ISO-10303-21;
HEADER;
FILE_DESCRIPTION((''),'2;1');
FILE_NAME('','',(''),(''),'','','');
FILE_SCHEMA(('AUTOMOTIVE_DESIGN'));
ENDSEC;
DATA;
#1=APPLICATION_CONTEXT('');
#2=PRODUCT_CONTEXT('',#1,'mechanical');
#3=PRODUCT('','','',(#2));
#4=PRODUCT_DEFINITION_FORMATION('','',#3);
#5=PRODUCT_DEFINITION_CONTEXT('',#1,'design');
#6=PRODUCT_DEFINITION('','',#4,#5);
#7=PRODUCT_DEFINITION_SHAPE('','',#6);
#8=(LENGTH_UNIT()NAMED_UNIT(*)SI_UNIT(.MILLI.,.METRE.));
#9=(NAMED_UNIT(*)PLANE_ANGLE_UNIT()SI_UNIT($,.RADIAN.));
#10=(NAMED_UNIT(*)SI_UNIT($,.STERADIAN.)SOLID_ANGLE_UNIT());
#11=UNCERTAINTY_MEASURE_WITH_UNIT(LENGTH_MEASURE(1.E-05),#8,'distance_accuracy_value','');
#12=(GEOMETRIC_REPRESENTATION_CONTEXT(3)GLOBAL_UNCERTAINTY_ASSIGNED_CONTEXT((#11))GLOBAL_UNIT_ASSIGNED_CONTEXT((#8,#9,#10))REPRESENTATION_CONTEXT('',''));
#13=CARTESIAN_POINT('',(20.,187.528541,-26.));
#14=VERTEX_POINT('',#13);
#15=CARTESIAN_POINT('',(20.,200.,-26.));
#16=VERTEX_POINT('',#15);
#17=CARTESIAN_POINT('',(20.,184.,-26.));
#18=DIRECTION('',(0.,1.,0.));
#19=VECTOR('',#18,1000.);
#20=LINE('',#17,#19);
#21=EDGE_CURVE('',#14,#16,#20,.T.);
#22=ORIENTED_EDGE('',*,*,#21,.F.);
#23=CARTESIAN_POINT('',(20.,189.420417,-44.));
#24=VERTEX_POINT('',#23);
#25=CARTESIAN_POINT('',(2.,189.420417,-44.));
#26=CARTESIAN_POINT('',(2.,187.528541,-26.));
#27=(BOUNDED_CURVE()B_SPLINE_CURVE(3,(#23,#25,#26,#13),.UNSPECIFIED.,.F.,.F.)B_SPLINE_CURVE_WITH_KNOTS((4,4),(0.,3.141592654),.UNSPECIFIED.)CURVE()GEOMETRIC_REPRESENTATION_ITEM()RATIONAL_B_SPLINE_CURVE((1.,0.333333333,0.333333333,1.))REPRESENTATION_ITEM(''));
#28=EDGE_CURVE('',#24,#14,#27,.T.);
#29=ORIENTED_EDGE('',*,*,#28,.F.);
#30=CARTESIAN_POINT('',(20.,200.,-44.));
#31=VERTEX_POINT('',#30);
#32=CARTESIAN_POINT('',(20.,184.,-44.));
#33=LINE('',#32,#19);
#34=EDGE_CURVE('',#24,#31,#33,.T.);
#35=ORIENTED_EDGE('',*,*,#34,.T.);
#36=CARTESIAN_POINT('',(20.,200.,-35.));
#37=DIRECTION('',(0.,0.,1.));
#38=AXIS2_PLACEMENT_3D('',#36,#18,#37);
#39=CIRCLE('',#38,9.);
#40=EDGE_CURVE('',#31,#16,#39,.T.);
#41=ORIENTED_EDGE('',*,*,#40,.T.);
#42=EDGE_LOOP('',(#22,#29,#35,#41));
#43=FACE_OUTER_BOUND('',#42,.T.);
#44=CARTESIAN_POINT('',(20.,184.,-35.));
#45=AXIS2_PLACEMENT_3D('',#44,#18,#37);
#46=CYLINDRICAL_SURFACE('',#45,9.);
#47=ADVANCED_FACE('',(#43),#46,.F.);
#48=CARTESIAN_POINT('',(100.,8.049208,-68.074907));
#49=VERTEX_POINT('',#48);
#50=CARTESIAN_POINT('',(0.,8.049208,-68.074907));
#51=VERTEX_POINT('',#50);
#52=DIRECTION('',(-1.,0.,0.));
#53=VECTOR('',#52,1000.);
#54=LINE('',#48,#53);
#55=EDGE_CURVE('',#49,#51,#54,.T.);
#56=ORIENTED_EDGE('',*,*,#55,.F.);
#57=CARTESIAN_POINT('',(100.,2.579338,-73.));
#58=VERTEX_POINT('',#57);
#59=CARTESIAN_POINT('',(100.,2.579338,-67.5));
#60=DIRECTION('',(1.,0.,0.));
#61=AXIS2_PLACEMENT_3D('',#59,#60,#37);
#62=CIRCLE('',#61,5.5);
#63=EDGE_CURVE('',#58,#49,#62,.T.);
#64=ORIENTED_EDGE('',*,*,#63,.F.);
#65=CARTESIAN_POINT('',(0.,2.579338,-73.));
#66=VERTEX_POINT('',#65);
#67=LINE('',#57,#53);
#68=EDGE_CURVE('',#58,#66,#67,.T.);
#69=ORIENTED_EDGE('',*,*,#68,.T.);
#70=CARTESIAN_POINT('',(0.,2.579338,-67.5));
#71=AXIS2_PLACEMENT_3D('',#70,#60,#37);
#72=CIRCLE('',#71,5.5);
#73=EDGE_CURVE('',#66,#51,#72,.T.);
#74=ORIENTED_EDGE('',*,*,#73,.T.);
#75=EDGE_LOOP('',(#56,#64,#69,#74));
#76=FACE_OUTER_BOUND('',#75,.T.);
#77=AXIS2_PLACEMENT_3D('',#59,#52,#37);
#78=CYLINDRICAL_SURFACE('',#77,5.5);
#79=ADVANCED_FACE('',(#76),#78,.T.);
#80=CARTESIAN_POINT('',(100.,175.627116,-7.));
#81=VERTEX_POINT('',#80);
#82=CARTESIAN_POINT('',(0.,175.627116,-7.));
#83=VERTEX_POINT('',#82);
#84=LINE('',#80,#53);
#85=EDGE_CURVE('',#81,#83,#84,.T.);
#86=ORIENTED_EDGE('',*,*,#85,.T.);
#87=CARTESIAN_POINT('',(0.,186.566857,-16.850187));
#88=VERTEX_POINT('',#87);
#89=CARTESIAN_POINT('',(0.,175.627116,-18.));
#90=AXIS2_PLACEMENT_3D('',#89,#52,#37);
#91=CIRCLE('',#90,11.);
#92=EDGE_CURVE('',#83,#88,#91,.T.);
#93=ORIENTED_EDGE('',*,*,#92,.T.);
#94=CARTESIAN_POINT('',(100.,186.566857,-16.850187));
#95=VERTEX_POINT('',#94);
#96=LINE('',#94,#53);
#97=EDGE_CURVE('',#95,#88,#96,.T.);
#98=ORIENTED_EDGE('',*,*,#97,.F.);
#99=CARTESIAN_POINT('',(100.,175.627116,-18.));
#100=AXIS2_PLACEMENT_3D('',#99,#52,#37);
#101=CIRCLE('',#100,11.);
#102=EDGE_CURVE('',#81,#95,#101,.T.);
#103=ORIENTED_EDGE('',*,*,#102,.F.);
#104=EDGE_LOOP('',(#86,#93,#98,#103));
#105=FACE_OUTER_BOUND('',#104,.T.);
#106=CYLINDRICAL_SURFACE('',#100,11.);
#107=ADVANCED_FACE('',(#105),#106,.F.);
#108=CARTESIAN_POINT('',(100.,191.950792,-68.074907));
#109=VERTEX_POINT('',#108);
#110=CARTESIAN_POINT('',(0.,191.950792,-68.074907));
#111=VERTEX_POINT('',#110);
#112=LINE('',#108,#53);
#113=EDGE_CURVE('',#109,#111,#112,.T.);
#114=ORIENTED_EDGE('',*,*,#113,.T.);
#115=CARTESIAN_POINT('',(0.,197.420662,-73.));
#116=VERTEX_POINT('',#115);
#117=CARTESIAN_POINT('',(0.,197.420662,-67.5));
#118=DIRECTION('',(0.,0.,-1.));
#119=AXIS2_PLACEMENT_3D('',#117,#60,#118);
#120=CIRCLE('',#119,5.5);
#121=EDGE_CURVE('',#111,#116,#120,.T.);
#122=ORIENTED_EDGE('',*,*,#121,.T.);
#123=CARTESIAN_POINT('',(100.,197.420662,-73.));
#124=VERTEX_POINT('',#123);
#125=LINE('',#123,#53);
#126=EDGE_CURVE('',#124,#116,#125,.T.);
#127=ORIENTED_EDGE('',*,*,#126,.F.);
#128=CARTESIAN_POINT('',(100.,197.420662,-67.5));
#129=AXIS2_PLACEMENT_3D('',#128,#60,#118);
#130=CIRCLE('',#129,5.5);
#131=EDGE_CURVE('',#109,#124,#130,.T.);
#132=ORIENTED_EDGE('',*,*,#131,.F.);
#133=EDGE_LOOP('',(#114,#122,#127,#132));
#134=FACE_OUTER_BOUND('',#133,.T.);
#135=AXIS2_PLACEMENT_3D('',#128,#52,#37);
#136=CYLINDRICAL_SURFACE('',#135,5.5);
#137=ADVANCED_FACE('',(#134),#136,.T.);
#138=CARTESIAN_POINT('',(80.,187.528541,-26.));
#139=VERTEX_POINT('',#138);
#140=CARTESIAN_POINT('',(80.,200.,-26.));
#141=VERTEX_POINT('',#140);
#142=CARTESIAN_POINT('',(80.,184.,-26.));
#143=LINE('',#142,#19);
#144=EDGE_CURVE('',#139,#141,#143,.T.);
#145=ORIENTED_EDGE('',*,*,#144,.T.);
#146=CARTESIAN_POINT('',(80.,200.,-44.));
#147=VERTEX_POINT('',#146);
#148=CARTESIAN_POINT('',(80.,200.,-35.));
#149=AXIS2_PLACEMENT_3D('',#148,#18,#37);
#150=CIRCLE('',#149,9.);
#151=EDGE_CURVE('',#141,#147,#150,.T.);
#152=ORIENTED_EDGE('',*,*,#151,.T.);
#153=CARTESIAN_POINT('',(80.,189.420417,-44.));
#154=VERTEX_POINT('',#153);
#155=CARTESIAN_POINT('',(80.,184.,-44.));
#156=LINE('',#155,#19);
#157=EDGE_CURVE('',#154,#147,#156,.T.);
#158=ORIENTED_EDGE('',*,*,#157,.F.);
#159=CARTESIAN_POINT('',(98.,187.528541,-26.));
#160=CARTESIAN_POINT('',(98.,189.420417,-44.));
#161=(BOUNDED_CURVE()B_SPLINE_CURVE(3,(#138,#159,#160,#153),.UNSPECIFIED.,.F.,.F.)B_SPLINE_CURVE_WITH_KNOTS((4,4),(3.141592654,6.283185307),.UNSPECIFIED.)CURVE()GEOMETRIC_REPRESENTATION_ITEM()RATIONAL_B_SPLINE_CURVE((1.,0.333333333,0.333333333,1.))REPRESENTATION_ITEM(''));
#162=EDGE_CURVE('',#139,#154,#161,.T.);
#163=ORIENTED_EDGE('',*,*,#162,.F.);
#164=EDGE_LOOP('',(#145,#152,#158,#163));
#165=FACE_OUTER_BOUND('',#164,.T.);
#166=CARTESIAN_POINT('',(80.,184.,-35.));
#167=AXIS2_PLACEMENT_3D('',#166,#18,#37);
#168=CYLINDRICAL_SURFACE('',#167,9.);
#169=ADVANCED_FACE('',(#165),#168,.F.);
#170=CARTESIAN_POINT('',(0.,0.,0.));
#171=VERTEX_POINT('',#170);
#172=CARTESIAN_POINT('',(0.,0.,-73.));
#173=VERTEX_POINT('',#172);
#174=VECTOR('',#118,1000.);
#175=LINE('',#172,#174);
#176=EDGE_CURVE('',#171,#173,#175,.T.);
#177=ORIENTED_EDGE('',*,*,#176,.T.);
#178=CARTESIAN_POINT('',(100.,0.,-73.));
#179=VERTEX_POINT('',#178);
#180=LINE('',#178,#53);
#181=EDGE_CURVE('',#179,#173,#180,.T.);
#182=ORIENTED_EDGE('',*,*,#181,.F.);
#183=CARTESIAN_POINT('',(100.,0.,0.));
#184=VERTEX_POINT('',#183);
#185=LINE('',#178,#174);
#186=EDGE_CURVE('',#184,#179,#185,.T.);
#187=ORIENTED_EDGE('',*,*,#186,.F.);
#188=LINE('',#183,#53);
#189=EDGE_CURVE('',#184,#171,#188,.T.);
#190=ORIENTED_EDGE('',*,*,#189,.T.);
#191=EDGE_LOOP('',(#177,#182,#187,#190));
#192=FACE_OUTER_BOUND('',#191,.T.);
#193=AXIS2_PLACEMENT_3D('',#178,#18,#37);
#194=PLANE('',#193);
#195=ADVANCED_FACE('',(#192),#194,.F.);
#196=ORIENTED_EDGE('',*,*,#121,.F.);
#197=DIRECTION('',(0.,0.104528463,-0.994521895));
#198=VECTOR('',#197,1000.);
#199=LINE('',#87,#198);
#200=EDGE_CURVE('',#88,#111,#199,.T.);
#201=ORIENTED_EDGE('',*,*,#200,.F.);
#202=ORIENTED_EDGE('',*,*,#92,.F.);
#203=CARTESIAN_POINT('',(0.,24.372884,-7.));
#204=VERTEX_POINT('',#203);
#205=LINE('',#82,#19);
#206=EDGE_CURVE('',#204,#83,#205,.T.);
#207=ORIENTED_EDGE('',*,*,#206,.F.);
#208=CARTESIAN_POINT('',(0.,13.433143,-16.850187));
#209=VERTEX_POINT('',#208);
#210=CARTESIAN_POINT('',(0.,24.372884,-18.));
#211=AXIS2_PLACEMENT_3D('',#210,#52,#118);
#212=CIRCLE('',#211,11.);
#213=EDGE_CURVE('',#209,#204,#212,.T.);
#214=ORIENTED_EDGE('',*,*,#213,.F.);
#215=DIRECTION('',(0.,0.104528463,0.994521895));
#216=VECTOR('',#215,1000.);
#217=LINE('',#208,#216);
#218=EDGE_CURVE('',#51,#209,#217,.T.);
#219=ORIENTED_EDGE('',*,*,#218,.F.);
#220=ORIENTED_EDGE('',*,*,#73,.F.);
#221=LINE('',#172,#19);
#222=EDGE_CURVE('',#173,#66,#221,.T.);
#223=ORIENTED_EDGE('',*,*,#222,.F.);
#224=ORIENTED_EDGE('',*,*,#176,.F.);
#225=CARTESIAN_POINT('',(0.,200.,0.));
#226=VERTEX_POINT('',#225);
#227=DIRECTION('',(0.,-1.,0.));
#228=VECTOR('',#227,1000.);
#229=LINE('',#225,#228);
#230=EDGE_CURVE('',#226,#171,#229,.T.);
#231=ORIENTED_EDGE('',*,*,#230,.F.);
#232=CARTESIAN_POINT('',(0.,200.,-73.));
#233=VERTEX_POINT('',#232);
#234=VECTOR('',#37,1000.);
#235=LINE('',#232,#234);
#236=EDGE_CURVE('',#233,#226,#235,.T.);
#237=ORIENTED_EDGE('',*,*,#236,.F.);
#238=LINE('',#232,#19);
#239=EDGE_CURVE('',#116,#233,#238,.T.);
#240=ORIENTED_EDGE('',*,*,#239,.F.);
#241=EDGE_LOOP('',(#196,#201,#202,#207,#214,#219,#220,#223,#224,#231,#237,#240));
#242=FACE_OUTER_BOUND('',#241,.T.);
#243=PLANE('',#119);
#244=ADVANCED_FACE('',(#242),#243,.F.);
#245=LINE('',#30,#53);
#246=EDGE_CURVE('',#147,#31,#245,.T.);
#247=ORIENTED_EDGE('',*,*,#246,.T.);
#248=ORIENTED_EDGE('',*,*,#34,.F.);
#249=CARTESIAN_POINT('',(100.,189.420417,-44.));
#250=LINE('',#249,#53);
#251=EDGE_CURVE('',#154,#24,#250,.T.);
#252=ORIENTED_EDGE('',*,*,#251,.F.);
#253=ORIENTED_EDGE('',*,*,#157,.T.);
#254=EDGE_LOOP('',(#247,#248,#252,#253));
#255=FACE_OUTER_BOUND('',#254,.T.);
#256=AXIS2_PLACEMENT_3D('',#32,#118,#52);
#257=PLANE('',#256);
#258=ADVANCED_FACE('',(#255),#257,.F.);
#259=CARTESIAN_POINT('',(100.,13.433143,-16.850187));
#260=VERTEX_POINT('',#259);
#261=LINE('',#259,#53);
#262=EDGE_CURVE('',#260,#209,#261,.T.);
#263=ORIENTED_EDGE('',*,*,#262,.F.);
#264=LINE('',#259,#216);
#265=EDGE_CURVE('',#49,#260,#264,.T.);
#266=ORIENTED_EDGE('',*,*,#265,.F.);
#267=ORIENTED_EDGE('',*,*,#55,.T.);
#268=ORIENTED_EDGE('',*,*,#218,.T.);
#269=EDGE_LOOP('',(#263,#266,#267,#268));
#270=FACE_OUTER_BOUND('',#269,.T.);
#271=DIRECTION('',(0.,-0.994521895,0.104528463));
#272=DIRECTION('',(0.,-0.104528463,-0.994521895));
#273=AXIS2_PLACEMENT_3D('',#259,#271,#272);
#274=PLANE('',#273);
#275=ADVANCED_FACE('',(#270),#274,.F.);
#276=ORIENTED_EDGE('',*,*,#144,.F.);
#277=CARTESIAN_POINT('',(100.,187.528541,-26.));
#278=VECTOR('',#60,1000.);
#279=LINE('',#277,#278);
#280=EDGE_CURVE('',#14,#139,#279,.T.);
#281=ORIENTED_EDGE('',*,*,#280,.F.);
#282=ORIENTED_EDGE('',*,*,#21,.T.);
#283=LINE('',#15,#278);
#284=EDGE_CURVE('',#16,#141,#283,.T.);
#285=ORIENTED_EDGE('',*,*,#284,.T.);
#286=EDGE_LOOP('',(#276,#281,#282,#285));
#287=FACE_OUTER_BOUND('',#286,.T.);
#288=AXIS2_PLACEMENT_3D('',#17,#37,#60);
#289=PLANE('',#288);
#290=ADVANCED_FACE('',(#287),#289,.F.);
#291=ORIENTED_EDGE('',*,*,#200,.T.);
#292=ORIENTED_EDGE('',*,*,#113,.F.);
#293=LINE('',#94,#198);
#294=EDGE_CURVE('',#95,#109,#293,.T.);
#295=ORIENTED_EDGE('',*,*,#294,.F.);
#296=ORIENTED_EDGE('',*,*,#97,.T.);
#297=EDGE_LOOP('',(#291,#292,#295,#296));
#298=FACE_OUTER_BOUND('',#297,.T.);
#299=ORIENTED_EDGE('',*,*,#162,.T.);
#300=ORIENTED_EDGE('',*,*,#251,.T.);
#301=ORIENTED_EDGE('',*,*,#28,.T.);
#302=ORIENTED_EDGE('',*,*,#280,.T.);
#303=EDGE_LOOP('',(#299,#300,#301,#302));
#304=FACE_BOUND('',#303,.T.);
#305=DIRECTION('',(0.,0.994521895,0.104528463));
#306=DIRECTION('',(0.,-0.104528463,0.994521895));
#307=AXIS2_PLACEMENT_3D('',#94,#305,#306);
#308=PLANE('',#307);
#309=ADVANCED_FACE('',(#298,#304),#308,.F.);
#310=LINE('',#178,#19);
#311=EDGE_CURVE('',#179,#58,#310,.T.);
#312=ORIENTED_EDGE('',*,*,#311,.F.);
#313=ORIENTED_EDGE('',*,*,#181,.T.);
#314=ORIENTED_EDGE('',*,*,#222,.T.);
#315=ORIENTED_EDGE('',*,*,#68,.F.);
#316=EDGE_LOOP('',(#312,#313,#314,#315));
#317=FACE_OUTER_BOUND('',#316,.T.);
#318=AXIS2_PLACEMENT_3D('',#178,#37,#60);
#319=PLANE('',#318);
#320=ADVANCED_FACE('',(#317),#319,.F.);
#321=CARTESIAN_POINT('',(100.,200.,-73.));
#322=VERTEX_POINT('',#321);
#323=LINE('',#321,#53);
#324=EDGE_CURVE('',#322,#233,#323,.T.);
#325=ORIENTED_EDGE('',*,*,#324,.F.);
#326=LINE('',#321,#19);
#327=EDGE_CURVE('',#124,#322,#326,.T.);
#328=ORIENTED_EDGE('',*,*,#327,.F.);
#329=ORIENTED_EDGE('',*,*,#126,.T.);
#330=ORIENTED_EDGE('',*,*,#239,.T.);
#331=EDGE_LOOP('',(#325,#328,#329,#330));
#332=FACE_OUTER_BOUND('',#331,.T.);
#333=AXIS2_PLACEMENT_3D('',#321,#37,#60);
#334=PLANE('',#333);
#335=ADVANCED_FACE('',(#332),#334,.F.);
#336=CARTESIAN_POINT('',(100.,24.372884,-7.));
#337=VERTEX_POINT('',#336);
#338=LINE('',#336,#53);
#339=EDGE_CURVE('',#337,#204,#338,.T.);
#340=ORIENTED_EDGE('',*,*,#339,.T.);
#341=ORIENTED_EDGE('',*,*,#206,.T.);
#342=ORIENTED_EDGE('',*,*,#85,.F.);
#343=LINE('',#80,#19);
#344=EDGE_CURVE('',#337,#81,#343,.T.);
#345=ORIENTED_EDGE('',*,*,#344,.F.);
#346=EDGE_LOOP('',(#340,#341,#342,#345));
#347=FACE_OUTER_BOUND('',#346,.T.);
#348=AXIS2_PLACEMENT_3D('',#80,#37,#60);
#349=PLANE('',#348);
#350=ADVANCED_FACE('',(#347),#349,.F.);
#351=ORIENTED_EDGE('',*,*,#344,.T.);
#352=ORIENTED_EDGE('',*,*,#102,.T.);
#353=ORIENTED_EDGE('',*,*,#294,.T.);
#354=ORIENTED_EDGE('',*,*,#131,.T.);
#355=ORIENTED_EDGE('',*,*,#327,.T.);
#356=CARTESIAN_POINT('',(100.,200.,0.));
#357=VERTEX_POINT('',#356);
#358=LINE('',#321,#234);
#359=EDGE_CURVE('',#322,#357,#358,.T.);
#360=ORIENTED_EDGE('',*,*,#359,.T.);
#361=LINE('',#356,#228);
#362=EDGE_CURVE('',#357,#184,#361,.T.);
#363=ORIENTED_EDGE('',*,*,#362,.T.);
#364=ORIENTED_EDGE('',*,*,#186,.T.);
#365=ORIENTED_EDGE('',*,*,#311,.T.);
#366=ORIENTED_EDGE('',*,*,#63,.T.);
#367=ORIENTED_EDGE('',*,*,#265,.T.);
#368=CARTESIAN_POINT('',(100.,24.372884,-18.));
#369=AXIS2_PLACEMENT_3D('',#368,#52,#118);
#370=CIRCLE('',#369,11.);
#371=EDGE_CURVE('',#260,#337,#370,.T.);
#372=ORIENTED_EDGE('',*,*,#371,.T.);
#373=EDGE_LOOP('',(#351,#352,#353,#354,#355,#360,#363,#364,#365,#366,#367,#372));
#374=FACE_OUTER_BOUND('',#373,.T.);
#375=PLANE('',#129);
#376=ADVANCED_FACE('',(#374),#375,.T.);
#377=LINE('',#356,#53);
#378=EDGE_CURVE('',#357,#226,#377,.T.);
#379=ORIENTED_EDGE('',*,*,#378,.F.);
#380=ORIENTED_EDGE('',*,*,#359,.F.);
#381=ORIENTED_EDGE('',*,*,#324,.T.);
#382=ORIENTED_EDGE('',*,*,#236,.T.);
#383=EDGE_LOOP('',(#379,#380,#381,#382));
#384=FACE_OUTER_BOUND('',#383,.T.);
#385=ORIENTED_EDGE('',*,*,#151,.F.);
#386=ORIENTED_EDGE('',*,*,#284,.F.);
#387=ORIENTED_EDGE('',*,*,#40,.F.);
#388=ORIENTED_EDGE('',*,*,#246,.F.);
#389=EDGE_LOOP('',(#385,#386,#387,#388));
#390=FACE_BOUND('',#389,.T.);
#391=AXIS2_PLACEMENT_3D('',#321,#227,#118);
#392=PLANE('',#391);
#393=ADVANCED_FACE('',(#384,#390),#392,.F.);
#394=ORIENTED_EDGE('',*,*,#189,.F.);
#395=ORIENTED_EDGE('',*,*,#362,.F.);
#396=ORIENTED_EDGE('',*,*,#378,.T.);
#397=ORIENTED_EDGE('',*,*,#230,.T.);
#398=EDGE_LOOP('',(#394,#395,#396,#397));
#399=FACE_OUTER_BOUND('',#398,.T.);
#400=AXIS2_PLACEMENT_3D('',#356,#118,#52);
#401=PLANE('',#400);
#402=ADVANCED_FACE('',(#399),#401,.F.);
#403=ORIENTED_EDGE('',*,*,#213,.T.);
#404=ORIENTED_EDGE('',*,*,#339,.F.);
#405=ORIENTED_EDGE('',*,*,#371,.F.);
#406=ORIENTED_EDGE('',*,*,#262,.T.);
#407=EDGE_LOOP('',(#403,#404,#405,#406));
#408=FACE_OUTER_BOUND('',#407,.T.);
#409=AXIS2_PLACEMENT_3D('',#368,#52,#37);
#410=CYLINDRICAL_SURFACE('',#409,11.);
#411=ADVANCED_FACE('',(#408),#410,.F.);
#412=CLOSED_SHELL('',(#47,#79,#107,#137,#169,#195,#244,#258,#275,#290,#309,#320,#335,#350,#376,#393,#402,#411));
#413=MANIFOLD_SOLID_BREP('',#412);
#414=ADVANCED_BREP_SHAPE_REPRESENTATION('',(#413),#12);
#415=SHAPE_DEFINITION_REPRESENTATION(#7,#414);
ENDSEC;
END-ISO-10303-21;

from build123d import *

# Parameters (mm, degrees)
C_20A_1_DEPTH       = 100
CUT_EXTRUDE_1_DEPTH = 16


with BuildPart() as part:
    # Sketch1 → C 槽 20A(1) (new body)
    with BuildSketch(Plane(origin=(0, 0, 0), x_dir=(0, 0, -1), z_dir=(1, 0, 0))):
        with BuildLine():
            Line((73, 200), (0, 200))
            Line((0, 200), (0, 0))
            Line((0, 0), (73, 0))
            Line((73, 0), (73, 2.579337993))
            ThreePointArc((73, 2.579337993), (71.58729654, 6.259556328), (68.074906548, 8.049208417))
            Line((68.074906548, 8.049208417), (16.850186904, 13.433143402))
            ThreePointArc((16.850186904, 13.433143402), (9.82540692, 17.012447581), (7, 24.372884251))
            Line((7, 24.372884251), (7, 175.627115749))
            ThreePointArc((7, 175.627115749), (9.82540692, 182.987552419), (16.850186904, 186.566856598))
            Line((16.850186904, 186.566856598), (68.074906548, 191.950791583))
            ThreePointArc((68.074906548, 191.950791583), (71.58729654, 193.740443672), (73, 197.420662007))
            Line((73, 197.420662007), (73, 200))
        make_face()
    extrude(amount=C_20A_1_DEPTH)

    # 草图2 → 切除-拉伸1 (cut)
    with BuildSketch(Plane(origin=(0, 200, 0), x_dir=(1, 0, 0), z_dir=(0, 1, 0))):
        with BuildLine():
            Line((20, 44), (80, 44))
            ThreePointArc((80, 44), (89, 35), (80, 26))
            Line((80, 26), (20, 26))
            ThreePointArc((20, 26), (11, 35), (20, 44))
        make_face()
    extrude(amount=-CUT_EXTRUDE_1_DEPTH, mode=Mode.SUBTRACT)


solid = part.part
